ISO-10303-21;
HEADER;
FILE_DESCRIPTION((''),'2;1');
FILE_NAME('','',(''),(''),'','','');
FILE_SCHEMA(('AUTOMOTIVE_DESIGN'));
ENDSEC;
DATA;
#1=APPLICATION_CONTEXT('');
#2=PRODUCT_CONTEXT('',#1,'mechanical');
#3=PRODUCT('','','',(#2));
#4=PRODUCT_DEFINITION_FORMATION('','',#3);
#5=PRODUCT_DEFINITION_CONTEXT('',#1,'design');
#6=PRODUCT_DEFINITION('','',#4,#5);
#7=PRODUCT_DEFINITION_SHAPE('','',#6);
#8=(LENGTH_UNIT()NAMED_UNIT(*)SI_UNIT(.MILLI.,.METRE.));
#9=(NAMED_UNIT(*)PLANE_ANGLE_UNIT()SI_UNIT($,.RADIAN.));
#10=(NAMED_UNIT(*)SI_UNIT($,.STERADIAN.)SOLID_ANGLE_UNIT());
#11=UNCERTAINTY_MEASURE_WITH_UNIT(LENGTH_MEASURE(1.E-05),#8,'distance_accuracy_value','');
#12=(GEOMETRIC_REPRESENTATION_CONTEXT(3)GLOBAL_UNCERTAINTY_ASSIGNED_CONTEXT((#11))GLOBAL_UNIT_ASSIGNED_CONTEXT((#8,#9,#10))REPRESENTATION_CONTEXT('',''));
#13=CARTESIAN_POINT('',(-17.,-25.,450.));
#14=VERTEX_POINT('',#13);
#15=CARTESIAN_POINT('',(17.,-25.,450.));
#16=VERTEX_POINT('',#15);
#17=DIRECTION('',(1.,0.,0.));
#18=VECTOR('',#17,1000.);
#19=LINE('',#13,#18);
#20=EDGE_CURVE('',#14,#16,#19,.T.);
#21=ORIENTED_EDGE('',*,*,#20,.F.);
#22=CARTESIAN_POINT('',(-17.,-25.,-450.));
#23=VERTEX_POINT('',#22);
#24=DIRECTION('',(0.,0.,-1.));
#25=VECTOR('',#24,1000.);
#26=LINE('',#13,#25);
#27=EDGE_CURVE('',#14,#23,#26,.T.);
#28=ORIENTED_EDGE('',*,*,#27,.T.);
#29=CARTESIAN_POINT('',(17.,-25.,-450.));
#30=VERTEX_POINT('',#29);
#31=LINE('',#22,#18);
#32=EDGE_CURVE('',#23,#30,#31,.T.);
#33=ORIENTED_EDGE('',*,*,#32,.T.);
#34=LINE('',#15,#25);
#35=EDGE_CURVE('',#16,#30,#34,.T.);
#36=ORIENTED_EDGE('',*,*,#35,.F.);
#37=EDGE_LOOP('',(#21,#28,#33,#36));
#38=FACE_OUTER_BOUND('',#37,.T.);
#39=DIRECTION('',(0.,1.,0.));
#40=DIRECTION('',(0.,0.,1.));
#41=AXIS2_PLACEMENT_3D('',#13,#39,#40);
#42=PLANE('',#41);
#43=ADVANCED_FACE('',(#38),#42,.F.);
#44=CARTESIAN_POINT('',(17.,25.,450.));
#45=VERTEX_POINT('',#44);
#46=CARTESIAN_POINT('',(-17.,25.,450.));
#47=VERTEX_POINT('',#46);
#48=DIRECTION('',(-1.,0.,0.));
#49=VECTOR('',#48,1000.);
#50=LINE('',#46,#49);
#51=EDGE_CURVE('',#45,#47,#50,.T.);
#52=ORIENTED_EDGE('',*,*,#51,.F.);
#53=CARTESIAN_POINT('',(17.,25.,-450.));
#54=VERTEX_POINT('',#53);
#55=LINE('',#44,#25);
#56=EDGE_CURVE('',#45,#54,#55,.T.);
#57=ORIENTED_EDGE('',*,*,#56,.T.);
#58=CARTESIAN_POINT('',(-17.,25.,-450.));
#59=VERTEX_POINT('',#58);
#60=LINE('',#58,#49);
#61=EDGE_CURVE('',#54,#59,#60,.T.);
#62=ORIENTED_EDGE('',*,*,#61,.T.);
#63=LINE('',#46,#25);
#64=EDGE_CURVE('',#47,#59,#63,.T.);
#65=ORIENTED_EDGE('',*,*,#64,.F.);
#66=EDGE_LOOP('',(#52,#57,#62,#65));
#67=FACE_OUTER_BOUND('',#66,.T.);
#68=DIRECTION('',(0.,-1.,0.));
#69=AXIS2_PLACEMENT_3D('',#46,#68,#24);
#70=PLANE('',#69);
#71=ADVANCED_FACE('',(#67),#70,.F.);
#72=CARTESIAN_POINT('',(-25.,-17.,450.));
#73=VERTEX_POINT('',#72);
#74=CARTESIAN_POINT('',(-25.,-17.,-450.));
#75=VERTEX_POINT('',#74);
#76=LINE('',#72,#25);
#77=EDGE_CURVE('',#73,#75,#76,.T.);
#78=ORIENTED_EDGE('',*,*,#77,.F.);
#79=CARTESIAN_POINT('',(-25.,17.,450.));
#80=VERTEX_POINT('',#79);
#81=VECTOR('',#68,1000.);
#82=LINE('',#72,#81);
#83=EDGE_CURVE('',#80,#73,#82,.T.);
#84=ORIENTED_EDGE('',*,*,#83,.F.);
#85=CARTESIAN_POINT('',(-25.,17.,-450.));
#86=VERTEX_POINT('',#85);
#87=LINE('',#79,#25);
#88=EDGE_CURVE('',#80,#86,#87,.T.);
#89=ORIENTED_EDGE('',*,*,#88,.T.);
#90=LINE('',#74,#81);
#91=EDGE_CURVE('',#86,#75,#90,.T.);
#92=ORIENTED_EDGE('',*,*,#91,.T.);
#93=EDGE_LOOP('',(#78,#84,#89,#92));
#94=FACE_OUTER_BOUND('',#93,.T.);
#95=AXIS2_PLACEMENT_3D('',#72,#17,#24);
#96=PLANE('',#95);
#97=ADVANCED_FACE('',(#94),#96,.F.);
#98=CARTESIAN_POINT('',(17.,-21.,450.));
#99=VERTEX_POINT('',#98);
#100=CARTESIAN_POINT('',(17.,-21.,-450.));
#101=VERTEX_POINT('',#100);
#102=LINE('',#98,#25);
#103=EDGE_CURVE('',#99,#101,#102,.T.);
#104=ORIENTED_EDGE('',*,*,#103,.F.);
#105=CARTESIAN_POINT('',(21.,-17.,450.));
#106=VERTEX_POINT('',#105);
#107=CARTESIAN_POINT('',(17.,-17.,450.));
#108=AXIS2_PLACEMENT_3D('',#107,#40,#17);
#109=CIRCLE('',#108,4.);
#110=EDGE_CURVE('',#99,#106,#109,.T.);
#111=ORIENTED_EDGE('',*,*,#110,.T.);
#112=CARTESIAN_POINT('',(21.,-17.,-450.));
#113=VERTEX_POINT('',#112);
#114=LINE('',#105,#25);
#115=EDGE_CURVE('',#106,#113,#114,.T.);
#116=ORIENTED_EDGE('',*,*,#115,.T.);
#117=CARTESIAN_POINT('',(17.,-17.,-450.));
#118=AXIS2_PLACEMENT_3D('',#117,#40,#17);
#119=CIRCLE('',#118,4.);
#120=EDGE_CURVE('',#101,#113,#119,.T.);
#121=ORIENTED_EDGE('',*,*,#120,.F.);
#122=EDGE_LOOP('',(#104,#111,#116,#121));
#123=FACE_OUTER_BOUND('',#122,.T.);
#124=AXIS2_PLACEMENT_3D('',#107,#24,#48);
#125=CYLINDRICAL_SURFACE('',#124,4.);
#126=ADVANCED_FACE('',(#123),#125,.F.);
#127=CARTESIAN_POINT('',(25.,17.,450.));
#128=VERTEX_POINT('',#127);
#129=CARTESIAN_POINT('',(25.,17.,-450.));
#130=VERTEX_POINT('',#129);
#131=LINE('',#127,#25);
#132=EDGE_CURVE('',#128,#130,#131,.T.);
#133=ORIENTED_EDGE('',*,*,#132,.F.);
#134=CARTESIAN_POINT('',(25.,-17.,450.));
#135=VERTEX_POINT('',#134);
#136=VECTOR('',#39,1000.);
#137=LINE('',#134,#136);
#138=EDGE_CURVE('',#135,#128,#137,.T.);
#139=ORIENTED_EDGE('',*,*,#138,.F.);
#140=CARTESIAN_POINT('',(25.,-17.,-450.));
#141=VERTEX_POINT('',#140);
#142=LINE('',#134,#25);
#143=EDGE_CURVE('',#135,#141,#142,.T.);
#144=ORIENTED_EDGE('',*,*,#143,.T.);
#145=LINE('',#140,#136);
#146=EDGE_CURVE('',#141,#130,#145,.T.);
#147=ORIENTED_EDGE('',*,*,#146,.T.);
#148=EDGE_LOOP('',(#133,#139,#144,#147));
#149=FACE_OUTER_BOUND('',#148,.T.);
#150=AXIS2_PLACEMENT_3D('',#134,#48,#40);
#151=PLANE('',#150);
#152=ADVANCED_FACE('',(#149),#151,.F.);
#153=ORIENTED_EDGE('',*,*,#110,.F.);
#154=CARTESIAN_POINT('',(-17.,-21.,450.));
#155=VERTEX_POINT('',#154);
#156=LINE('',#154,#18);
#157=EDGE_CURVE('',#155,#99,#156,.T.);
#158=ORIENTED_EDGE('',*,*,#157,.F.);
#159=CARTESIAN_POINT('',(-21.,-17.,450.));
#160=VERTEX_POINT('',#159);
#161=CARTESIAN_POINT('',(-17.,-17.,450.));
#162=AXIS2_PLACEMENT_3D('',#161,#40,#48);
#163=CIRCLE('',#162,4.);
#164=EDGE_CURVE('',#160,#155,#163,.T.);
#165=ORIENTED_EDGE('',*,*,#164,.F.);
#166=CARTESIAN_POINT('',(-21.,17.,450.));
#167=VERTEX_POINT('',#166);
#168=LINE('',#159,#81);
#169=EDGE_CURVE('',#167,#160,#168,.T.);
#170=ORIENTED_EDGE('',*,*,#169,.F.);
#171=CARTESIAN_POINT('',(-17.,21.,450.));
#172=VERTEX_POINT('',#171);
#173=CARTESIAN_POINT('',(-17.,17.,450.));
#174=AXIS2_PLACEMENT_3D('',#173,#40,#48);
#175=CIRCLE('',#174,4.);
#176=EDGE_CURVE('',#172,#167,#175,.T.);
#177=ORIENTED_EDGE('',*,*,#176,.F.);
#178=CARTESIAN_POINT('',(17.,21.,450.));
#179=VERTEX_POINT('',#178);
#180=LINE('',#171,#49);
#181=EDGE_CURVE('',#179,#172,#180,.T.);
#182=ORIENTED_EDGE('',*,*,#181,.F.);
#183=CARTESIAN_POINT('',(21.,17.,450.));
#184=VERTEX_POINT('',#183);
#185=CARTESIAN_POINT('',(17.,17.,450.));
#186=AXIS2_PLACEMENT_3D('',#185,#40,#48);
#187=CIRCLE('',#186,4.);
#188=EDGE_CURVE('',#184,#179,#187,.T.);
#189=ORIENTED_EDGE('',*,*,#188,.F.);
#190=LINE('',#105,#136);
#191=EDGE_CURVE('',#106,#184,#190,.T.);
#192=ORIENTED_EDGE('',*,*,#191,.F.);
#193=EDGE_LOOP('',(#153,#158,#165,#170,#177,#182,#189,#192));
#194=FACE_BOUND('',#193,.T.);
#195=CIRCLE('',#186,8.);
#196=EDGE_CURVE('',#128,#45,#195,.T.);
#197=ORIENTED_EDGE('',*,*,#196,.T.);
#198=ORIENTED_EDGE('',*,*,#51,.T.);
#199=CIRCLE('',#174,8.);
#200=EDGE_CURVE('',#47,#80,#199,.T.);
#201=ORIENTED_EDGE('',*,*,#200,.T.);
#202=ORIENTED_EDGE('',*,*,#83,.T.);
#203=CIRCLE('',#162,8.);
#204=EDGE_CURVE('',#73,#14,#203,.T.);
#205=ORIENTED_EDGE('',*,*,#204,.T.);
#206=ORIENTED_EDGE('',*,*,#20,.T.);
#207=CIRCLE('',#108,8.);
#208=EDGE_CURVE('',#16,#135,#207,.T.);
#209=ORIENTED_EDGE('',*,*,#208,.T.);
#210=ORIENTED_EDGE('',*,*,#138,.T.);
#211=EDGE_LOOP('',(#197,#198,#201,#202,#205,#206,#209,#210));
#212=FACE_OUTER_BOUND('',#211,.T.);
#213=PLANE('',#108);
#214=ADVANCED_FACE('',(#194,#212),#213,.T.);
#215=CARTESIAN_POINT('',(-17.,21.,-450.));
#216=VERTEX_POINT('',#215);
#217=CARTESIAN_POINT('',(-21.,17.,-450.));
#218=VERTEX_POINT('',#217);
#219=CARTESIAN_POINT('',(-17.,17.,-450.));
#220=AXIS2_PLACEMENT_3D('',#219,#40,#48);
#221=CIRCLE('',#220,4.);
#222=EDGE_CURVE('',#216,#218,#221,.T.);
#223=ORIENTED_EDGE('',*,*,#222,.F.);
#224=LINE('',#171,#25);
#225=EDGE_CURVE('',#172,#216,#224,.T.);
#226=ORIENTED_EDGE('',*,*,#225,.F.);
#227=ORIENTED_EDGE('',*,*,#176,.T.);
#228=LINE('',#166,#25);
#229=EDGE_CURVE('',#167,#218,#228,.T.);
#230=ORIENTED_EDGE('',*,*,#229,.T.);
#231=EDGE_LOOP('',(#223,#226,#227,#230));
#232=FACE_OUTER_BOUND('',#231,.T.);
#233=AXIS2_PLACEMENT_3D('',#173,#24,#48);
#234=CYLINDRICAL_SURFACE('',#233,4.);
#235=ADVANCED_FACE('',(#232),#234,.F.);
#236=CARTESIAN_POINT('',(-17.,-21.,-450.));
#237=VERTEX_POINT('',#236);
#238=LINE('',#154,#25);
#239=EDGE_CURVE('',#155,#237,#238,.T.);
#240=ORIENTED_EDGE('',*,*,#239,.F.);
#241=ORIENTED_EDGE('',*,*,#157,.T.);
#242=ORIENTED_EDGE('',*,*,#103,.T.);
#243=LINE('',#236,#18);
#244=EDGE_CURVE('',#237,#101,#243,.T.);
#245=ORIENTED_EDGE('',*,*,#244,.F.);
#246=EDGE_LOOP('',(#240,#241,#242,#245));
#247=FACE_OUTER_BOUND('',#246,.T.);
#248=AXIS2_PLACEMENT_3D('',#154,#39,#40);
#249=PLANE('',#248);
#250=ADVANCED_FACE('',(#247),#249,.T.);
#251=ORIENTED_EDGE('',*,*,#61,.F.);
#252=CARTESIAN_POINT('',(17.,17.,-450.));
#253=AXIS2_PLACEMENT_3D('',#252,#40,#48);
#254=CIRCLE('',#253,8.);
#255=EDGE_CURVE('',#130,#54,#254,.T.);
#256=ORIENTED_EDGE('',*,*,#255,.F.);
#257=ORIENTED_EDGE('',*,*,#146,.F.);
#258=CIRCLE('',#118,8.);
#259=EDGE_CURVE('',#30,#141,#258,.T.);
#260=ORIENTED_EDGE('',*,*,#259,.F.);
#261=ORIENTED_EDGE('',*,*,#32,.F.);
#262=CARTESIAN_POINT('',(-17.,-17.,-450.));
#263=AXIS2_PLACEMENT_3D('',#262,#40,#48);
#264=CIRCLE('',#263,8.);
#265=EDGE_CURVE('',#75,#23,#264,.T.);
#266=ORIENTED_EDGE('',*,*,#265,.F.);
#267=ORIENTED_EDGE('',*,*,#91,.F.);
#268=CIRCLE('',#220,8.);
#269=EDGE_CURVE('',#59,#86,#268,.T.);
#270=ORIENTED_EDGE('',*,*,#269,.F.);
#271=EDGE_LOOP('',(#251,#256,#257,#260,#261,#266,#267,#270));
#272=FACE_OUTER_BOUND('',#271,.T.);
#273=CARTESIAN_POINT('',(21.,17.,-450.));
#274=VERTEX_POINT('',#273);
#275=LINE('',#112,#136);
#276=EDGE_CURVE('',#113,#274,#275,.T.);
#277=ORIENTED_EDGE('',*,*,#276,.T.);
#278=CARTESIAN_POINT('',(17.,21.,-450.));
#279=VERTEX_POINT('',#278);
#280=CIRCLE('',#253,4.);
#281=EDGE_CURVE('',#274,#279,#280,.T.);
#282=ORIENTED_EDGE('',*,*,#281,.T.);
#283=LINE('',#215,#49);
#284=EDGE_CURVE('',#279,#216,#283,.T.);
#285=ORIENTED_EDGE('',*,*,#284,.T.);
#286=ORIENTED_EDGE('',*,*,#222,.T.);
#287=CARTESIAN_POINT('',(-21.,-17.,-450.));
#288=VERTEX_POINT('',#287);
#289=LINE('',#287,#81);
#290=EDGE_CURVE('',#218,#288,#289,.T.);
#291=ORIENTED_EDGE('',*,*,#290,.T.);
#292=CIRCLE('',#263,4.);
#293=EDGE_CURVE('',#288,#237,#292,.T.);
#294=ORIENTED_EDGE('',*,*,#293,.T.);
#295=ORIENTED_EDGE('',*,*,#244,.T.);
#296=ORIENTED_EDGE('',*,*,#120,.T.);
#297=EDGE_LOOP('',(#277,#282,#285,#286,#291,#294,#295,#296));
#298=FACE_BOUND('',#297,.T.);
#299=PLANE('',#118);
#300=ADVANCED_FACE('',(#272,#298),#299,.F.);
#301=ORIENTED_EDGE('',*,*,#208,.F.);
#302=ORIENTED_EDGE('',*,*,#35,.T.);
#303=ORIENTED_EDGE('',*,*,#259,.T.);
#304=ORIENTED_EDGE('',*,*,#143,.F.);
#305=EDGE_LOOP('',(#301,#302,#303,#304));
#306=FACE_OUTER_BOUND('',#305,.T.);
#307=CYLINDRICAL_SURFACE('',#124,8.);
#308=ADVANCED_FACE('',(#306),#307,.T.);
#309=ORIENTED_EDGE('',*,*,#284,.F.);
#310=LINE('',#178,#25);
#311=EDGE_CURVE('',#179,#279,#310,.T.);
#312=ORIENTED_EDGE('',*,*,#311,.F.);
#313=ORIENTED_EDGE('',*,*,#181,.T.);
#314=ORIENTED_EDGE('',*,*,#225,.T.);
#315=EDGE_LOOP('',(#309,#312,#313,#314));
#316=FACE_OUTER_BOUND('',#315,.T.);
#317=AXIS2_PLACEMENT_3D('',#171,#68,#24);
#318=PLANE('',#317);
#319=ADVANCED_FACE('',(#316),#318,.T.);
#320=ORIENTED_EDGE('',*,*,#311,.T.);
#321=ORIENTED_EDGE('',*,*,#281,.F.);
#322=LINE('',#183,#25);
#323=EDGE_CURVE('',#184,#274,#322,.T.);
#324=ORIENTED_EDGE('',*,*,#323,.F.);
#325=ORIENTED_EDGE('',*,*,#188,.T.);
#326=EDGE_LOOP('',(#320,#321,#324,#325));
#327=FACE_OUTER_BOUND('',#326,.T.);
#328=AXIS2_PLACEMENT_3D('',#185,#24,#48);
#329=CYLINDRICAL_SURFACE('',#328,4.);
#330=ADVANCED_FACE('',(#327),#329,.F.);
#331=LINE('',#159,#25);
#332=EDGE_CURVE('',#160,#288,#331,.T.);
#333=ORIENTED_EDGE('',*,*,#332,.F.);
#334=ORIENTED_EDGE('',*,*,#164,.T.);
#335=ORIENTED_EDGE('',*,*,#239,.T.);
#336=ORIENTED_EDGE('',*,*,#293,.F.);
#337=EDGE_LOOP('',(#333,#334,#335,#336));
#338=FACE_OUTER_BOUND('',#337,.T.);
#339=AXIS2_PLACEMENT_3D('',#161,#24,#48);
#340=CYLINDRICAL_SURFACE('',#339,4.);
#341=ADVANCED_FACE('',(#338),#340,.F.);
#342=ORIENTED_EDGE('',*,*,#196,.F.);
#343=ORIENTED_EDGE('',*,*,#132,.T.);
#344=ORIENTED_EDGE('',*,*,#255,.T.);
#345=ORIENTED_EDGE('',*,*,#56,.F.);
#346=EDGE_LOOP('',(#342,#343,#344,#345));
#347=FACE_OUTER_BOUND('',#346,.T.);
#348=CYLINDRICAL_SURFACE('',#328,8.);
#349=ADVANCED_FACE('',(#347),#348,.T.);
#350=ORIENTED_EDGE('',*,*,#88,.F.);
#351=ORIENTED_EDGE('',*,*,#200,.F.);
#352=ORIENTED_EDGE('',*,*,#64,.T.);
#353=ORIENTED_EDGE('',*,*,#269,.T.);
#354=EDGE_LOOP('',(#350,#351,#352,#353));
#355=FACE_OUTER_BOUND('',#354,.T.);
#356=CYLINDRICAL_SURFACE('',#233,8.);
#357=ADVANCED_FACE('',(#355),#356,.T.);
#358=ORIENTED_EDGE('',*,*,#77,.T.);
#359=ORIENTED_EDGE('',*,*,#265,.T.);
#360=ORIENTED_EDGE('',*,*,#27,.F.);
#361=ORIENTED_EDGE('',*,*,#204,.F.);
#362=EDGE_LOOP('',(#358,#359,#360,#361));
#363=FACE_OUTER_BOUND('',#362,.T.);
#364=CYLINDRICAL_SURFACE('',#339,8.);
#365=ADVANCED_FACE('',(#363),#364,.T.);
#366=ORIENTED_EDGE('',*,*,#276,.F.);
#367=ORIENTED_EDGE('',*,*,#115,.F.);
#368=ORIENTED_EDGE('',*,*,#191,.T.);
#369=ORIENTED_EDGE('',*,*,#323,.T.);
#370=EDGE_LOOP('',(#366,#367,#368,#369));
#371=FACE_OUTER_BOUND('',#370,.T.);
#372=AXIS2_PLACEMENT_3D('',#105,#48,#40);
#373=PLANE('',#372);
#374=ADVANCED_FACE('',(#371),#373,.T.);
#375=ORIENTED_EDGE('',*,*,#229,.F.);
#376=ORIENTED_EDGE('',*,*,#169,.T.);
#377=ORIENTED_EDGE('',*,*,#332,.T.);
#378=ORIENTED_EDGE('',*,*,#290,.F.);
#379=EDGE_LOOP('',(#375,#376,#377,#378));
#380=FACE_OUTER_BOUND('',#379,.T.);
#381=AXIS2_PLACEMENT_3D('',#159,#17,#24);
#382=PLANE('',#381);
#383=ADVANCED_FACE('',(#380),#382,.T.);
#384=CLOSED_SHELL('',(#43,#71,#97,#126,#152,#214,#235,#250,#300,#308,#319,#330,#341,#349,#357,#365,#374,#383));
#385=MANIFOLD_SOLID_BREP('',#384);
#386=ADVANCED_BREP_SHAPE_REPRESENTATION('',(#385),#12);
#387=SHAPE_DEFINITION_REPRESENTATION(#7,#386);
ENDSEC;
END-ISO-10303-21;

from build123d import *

# Parameters (mm, degrees)
BOSS_EXTRUDE1_DEPTH = 450


with BuildPart() as part:
    # Sketch1 → Boss-Extrude1 (new, symmetric)
    with BuildSketch(Plane.XY):
        with BuildLine():
            Line((-17, -25), (17, -25))
            ThreePointArc((17, -25), (22.656854249, -22.656854249), (25, -17))
            Line((25, -17), (25, 17))
            ThreePointArc((25, 17), (22.656854249, 22.656854249), (17, 25))
            Line((17, 25), (-17, 25))
            ThreePointArc((-17, 25), (-22.656854249, 22.656854249), (-25, 17))
            Line((-25, 17), (-25, -17))
            ThreePointArc((-25, -17), (-22.656854249, -22.656854249), (-17, -25))
        make_face()
        with BuildLine():
            Line((-17, 21), (17, 21))
            ThreePointArc((17, 21), (19.828427125, 19.828427125), (21, 17))
            Line((21, 17), (21, -17))
            ThreePointArc((21, -17), (19.828427125, -19.828427125), (17, -21))
            Line((17, -21), (-17, -21))
            ThreePointArc((-17, -21), (-19.828427125, -19.828427125), (-21, -17))
            Line((-21, -17), (-21, 17))
            ThreePointArc((-21, 17), (-19.828427125, 19.828427125), (-17, 21))
        make_face(mode=Mode.SUBTRACT)
    extrude(amount=BOSS_EXTRUDE1_DEPTH, both=True)


solid = part.part
